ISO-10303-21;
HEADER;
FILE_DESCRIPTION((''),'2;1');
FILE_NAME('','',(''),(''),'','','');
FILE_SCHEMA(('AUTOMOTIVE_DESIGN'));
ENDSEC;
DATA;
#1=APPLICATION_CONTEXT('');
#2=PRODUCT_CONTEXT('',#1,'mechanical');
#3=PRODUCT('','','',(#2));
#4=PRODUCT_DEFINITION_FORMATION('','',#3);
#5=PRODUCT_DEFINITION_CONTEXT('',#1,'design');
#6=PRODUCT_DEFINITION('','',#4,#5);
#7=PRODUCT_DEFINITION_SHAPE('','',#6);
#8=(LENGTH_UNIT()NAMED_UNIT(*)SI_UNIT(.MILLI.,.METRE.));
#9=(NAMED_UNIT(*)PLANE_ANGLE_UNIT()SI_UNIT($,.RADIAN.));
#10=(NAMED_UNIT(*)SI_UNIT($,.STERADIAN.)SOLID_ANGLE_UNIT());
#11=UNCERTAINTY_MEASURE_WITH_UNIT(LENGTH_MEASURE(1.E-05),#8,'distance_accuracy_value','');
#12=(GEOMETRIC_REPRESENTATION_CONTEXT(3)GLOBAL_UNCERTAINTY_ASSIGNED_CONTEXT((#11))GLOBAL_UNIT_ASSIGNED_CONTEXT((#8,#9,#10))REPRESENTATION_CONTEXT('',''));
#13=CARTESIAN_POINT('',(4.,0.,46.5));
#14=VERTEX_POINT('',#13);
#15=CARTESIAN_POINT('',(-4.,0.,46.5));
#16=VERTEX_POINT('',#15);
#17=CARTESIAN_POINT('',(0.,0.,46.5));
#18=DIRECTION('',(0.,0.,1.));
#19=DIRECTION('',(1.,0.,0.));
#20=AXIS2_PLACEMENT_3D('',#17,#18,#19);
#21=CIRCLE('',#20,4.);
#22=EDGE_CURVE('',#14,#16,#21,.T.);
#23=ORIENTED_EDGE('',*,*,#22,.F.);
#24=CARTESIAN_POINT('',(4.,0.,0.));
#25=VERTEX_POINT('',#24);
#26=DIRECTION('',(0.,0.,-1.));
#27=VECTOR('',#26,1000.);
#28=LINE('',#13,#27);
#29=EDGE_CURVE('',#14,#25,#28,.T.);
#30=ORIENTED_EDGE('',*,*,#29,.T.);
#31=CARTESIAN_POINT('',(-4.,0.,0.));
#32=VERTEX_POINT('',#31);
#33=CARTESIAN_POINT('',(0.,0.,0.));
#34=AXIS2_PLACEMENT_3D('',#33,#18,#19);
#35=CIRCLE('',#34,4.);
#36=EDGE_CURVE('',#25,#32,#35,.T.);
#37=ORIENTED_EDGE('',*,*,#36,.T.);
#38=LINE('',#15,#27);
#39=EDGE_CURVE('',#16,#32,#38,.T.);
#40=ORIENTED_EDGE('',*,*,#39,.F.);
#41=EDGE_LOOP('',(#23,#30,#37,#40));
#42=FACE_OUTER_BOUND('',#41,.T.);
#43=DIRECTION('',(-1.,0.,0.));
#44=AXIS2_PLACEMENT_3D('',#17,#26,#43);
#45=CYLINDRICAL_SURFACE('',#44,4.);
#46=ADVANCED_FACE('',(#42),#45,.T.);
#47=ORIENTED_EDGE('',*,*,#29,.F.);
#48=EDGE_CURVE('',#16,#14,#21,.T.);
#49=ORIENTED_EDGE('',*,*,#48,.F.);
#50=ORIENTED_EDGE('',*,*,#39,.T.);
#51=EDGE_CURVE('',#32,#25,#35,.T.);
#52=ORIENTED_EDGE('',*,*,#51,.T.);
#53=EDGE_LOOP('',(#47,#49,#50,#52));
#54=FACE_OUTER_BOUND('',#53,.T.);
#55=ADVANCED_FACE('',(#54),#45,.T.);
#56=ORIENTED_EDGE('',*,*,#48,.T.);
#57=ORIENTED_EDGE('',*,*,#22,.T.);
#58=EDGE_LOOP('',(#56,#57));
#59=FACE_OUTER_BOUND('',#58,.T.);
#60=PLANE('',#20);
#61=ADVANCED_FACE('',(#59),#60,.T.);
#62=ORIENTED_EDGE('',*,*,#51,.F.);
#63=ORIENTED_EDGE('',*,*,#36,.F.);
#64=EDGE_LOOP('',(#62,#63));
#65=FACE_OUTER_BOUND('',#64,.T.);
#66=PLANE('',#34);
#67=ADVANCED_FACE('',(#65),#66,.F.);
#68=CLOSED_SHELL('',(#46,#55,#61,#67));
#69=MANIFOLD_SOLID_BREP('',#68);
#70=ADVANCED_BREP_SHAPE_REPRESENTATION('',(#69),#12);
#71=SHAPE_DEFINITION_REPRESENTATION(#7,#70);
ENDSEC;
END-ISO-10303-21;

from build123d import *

# Parameters (mm, degrees)
SKETCH1_R           = 4
BOSS_EXTRUDE1_DEPTH = 46.5


with BuildPart() as part:
    # Sketch1 → Boss-Extrude1 (new body)
    with BuildSketch(Plane.XY):
        with Locations(Location((0, 0, 0), (0, 0, 180))):
            Circle(SKETCH1_R)
    extrude(amount=BOSS_EXTRUDE1_DEPTH)


solid = part.part
